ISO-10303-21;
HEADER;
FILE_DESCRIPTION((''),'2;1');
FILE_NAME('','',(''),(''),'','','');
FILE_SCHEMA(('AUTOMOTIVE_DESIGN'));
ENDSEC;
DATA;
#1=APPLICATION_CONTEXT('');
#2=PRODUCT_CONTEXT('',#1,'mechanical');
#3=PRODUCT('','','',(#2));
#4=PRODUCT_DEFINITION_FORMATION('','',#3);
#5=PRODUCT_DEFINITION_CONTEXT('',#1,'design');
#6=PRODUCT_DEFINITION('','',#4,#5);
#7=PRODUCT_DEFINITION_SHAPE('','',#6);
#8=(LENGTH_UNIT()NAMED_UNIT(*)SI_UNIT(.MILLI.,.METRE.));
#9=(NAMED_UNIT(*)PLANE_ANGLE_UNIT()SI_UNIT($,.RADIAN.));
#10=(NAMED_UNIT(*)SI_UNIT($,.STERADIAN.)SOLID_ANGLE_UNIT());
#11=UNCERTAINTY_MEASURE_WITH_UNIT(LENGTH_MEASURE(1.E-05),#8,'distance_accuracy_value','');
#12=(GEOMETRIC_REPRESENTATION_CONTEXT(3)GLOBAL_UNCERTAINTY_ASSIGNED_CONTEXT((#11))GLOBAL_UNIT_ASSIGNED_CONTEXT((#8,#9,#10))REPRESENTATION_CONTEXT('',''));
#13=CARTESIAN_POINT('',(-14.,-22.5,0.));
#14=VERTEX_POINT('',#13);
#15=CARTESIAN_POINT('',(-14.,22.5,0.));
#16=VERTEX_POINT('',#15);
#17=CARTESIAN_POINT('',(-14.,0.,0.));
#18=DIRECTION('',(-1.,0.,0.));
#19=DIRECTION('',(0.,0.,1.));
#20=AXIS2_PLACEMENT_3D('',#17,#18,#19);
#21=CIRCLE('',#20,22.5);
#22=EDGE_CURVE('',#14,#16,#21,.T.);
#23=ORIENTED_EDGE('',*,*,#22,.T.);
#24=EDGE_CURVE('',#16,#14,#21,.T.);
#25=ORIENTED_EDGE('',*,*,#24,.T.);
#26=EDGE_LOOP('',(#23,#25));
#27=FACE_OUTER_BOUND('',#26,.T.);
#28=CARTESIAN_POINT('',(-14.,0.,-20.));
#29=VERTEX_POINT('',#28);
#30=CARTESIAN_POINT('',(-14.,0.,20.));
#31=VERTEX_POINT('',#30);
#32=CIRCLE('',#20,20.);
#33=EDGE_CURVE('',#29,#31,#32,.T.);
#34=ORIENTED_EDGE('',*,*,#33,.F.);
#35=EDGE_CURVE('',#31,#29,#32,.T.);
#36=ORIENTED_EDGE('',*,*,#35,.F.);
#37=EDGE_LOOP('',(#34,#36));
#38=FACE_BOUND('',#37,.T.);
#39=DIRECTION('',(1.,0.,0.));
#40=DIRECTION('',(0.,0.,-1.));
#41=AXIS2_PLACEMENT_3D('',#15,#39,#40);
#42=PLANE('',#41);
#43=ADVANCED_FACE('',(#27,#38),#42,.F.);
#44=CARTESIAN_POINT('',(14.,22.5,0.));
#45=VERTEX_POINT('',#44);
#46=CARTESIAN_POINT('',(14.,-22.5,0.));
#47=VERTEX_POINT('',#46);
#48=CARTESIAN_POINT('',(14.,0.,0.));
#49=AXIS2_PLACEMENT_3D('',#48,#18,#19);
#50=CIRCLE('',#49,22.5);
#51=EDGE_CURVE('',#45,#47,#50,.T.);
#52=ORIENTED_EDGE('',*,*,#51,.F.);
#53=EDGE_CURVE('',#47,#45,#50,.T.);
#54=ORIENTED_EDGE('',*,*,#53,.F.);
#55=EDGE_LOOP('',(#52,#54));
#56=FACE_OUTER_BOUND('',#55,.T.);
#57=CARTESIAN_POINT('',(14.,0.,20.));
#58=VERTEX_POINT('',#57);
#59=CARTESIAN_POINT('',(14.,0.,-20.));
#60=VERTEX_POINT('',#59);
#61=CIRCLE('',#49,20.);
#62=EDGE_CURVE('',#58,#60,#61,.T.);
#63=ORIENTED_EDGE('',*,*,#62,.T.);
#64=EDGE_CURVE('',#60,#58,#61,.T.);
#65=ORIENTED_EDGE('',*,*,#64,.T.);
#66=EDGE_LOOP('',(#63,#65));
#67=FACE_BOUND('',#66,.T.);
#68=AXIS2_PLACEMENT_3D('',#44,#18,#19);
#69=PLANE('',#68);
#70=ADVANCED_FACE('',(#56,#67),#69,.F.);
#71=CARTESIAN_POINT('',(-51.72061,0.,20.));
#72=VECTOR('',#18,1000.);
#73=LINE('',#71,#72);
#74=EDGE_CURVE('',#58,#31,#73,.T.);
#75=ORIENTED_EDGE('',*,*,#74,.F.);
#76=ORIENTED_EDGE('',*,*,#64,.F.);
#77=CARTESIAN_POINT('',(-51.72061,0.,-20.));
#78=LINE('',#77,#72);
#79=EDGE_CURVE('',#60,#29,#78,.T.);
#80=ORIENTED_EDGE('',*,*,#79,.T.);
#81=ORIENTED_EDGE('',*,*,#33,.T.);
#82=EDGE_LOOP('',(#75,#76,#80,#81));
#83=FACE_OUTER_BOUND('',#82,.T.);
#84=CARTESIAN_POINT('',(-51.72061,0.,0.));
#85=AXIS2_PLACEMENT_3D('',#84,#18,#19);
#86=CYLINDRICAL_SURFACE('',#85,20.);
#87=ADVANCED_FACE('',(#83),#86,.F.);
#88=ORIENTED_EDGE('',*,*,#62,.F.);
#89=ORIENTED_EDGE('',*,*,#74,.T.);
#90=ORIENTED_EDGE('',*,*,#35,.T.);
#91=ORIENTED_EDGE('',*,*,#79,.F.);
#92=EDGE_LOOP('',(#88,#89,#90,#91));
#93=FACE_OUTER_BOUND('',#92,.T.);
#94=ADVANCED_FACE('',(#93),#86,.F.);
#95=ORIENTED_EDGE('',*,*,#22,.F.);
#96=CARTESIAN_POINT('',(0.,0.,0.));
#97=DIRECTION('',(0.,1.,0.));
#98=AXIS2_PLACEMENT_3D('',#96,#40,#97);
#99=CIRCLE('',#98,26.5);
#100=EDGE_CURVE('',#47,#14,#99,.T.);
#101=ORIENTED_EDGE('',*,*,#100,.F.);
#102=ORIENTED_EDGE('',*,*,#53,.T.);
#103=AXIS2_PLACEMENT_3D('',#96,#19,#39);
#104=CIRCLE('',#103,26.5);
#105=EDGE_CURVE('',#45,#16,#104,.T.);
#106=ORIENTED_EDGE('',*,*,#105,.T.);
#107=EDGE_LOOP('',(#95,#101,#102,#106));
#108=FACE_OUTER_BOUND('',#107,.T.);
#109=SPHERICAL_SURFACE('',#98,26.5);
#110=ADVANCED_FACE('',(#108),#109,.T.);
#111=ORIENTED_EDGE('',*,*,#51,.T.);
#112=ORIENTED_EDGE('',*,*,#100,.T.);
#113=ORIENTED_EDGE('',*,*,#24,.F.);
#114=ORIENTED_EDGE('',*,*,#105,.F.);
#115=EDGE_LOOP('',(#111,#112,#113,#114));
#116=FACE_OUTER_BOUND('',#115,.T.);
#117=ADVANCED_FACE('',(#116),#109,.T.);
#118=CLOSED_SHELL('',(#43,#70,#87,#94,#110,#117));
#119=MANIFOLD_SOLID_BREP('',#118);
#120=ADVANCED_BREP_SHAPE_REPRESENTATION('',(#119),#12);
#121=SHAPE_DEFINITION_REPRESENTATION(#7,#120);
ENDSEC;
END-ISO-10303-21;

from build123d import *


with BuildPart() as part:
    # 草图1 → 旋转1 (revolve)
    with BuildSketch(Plane.XY, mode=Mode.PRIVATE) as revolve_1_sk:
        with BuildLine():
            Line((-14, 22.5), (-14, 20))
            Line((-14, 20), (14, 20))
            Line((14, 20), (14, 22.5))
            ThreePointArc((14, 22.5), (0, 26.5), (-14, 22.5))
        make_face()
    revolve(revolve_1_sk.sketch.rotate(Axis((-51.72060984, 0, 0), (1, 0, 0)), 90), axis=Axis((-51.72060984, 0, 0), (1, 0, 0)))


solid = part.part
